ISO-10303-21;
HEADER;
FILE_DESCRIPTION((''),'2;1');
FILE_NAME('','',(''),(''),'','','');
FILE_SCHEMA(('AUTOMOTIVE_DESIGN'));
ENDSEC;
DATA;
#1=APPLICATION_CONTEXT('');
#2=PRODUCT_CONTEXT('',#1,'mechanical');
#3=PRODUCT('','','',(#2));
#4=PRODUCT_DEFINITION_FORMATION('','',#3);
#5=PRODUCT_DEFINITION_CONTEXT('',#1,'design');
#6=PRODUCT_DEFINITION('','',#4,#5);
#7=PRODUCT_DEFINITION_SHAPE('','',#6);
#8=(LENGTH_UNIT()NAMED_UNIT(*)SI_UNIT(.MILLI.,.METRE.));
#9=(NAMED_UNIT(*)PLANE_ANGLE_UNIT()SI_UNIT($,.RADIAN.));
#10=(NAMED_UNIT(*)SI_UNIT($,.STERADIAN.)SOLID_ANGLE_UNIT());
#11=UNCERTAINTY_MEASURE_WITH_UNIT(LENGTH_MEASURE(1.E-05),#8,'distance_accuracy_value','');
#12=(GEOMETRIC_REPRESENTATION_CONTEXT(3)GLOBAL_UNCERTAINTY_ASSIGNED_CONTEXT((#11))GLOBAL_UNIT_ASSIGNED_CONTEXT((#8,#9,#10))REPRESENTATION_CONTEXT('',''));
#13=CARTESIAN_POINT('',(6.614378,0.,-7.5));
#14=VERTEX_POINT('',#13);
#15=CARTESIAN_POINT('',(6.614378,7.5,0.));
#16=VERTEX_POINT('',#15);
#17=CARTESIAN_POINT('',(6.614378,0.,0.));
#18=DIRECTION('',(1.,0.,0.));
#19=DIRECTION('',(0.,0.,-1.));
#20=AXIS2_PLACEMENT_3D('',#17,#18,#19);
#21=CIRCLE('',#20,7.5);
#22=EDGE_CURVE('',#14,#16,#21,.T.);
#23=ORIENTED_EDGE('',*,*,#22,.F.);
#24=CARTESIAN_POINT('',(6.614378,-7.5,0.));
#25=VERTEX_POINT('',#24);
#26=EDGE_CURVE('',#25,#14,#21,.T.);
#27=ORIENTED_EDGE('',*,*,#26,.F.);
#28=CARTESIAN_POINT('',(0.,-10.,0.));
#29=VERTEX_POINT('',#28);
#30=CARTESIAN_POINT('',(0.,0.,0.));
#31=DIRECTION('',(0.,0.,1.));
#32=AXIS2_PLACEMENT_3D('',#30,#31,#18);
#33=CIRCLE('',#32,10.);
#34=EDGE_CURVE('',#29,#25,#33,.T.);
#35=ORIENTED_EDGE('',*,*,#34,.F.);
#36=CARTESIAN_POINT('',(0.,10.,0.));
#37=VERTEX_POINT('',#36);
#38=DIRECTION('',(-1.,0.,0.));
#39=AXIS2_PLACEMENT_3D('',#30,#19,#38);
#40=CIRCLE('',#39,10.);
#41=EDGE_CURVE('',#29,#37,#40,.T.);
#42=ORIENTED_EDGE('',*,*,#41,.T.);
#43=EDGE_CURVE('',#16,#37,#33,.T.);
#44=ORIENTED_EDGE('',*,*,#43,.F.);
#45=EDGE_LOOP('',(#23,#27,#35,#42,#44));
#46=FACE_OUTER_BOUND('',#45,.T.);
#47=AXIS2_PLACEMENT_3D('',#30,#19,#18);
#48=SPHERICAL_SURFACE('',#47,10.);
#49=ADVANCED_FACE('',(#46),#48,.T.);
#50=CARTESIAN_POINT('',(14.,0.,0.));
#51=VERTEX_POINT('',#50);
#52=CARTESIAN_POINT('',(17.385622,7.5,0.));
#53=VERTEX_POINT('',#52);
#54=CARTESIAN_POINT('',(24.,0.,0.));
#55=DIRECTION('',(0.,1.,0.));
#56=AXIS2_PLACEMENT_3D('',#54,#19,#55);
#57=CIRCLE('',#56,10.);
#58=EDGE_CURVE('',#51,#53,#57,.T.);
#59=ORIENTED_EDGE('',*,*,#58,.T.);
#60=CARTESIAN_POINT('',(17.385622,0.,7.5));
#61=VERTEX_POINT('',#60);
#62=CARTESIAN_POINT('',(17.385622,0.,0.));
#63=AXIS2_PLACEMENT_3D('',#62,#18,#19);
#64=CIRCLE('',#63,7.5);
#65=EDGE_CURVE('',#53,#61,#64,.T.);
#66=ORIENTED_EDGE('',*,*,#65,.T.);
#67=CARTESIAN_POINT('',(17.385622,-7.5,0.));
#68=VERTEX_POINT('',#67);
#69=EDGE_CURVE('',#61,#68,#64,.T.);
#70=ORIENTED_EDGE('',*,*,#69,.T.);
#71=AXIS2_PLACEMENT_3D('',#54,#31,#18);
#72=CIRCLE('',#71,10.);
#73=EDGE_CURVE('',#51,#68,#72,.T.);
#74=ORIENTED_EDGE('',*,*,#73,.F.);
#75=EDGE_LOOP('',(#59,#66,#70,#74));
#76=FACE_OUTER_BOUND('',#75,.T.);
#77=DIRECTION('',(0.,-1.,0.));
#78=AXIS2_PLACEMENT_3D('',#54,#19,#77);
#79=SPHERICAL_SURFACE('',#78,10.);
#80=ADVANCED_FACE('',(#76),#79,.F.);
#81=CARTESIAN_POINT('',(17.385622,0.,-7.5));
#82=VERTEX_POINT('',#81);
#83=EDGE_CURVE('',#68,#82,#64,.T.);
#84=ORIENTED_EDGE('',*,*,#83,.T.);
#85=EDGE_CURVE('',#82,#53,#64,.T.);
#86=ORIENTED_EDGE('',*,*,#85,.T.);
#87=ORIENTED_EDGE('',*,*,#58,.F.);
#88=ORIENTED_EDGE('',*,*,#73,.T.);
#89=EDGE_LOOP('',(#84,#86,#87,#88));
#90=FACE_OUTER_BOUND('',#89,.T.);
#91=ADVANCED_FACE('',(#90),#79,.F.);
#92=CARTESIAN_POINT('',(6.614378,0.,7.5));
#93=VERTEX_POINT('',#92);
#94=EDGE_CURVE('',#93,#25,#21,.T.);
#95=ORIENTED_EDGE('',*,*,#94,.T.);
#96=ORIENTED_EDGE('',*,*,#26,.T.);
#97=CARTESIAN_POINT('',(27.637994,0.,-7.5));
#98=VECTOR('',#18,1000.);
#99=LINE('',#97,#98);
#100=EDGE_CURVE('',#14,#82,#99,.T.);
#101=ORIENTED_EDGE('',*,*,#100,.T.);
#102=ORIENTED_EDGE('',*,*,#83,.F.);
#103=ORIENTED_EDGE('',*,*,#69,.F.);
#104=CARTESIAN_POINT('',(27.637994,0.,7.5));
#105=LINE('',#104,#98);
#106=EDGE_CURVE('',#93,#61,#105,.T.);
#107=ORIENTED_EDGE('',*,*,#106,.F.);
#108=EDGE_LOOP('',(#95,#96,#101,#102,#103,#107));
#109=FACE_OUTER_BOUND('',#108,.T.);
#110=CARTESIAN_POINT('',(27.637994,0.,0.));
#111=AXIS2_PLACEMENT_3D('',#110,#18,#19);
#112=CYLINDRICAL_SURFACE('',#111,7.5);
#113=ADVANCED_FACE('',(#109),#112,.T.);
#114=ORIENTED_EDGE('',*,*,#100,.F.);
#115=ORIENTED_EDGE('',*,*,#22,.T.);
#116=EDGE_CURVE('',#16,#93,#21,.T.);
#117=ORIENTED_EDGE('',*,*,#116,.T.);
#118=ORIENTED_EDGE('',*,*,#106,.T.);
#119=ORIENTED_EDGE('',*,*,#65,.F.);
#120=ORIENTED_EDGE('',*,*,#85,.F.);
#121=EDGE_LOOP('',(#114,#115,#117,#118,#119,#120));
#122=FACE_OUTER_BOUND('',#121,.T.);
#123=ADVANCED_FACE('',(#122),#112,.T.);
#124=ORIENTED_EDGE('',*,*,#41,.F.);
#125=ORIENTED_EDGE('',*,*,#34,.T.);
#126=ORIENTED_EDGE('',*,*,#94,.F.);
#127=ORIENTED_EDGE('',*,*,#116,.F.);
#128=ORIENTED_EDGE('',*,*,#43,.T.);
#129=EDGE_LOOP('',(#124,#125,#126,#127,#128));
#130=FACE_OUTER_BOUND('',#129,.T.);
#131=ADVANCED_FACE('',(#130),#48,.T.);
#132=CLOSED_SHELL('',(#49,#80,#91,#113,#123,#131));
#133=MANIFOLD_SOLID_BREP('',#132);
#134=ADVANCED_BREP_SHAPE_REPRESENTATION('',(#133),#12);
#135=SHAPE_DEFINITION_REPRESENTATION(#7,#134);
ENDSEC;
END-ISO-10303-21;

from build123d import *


with BuildPart() as part:
    # Sketch1 → Revolve3 (revolve)
    with BuildSketch(Plane.XY):
        with BuildLine():
            Line((0, 10), (0, -10))
            ThreePointArc((0, -10), (10, 0), (0, 10))
        make_face()
    revolve(axis=Axis((0, 23.790519838, 0), (0, -1, 0)))

    # Sketch2 → Revolve4 (revolve)
    with BuildSketch(Plane.XY, mode=Mode.PRIVATE) as revolve4_sk:
        with BuildLine():
            Line((6.614378278, 7.5), (17.385621722, 7.5))
            ThreePointArc((17.385621722, 7.5), (14.885621722, 4.114378278), (14, 0))
            Line((14, 0), (10, 0))
            ThreePointArc((10, 0), (9.114378278, 4.114378278), (6.614378278, 7.5))
        make_face()
    revolve(revolve4_sk.sketch.rotate(Axis((27.637994168, 0, 0), (-1, 0, 0)), 90), axis=Axis((27.637994168, 0, 0), (-1, 0, 0)))


solid = part.part
